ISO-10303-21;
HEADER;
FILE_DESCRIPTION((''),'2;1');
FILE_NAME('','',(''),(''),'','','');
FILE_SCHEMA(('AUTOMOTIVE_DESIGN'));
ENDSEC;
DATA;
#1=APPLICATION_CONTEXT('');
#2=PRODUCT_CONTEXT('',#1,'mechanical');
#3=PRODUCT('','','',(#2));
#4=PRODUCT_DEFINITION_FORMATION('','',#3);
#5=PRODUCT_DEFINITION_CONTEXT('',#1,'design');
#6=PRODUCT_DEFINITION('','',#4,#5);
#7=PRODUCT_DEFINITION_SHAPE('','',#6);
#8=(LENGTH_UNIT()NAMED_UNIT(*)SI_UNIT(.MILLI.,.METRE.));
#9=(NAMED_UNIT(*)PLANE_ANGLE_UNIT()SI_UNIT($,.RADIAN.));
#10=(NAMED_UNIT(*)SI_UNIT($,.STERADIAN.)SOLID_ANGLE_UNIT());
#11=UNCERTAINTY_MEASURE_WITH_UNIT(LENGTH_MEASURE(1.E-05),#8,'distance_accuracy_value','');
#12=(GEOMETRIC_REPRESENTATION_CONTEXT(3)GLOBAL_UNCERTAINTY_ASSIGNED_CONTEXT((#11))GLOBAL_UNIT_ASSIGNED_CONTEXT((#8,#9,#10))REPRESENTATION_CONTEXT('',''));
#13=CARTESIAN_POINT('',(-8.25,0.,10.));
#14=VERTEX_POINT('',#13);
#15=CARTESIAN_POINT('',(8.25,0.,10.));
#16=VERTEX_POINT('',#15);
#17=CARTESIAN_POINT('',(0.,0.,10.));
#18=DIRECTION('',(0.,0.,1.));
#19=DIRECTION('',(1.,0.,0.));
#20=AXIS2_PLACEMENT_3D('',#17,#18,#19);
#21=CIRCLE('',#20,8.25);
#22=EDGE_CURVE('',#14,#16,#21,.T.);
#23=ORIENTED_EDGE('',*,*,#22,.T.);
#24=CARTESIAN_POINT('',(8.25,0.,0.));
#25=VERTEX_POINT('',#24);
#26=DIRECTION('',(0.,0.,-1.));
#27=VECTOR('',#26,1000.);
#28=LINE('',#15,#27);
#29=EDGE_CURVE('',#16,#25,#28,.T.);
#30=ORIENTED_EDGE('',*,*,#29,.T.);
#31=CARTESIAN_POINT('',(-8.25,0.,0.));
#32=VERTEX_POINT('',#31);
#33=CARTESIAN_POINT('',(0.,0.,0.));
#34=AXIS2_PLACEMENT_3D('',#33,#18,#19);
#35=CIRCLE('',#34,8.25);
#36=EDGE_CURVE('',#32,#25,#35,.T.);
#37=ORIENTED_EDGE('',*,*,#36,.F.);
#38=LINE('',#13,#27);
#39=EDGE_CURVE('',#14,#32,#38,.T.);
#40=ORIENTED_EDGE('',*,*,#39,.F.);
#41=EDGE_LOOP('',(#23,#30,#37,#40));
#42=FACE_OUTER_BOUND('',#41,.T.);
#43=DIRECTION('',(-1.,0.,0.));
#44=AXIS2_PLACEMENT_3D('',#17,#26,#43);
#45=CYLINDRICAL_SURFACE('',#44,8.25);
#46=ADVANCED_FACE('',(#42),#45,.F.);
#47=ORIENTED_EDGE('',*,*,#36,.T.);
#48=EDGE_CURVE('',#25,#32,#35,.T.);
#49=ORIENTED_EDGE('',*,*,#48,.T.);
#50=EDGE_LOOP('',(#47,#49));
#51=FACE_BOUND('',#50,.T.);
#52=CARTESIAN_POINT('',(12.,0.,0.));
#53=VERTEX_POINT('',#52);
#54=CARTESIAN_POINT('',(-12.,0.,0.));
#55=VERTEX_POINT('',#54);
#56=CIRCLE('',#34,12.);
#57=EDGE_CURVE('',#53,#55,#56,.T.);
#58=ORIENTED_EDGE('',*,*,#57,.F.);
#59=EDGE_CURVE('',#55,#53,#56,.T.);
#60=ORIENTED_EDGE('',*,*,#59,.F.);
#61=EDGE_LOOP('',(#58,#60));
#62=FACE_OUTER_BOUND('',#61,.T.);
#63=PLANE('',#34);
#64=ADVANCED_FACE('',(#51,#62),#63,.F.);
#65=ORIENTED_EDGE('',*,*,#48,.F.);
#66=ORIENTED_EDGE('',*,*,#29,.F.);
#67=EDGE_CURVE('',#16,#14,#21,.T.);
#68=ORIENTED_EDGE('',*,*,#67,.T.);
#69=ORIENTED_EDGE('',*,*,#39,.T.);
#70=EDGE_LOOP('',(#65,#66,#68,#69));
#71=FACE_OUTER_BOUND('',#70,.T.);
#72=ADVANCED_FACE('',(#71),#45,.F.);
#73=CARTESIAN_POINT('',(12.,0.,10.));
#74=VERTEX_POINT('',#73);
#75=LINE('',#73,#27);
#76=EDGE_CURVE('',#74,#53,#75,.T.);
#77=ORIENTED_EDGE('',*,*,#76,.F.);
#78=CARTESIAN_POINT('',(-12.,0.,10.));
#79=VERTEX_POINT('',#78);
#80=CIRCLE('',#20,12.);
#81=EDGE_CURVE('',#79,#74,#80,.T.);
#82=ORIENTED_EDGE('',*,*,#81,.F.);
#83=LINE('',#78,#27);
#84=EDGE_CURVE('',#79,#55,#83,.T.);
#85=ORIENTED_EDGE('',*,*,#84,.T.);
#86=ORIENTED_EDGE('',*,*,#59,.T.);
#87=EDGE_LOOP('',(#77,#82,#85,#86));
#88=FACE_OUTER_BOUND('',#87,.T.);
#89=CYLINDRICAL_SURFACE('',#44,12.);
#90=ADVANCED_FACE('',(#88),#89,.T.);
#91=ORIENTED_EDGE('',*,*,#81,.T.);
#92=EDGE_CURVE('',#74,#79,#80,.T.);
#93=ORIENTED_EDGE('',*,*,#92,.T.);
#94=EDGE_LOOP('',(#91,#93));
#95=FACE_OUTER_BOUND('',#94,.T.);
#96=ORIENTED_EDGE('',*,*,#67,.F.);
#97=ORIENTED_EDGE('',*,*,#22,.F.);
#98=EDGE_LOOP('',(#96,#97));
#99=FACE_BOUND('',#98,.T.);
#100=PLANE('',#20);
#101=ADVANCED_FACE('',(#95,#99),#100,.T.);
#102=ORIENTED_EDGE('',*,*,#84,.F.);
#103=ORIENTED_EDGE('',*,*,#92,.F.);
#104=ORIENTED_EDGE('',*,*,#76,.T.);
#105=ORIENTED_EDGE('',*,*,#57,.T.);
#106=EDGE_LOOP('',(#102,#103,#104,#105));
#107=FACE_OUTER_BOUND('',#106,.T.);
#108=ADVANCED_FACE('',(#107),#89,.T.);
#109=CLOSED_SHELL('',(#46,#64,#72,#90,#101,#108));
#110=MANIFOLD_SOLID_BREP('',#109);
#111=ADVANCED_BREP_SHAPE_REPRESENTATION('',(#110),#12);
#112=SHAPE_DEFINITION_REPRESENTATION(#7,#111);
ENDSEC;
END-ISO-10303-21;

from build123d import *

# Parameters (mm, degrees)
SKETCH_1_R      = 12
SKETCH_1_R_2    = 8.25
EXTRUDE_1_DEPTH = 10


with BuildPart() as part:
    # 草图1 → 凸台-拉伸1 (new body)
    with BuildSketch(Plane.XY):
        Circle(SKETCH_1_R)
        Circle(SKETCH_1_R_2, mode=Mode.SUBTRACT)
    extrude(amount=EXTRUDE_1_DEPTH)


solid = part.part
